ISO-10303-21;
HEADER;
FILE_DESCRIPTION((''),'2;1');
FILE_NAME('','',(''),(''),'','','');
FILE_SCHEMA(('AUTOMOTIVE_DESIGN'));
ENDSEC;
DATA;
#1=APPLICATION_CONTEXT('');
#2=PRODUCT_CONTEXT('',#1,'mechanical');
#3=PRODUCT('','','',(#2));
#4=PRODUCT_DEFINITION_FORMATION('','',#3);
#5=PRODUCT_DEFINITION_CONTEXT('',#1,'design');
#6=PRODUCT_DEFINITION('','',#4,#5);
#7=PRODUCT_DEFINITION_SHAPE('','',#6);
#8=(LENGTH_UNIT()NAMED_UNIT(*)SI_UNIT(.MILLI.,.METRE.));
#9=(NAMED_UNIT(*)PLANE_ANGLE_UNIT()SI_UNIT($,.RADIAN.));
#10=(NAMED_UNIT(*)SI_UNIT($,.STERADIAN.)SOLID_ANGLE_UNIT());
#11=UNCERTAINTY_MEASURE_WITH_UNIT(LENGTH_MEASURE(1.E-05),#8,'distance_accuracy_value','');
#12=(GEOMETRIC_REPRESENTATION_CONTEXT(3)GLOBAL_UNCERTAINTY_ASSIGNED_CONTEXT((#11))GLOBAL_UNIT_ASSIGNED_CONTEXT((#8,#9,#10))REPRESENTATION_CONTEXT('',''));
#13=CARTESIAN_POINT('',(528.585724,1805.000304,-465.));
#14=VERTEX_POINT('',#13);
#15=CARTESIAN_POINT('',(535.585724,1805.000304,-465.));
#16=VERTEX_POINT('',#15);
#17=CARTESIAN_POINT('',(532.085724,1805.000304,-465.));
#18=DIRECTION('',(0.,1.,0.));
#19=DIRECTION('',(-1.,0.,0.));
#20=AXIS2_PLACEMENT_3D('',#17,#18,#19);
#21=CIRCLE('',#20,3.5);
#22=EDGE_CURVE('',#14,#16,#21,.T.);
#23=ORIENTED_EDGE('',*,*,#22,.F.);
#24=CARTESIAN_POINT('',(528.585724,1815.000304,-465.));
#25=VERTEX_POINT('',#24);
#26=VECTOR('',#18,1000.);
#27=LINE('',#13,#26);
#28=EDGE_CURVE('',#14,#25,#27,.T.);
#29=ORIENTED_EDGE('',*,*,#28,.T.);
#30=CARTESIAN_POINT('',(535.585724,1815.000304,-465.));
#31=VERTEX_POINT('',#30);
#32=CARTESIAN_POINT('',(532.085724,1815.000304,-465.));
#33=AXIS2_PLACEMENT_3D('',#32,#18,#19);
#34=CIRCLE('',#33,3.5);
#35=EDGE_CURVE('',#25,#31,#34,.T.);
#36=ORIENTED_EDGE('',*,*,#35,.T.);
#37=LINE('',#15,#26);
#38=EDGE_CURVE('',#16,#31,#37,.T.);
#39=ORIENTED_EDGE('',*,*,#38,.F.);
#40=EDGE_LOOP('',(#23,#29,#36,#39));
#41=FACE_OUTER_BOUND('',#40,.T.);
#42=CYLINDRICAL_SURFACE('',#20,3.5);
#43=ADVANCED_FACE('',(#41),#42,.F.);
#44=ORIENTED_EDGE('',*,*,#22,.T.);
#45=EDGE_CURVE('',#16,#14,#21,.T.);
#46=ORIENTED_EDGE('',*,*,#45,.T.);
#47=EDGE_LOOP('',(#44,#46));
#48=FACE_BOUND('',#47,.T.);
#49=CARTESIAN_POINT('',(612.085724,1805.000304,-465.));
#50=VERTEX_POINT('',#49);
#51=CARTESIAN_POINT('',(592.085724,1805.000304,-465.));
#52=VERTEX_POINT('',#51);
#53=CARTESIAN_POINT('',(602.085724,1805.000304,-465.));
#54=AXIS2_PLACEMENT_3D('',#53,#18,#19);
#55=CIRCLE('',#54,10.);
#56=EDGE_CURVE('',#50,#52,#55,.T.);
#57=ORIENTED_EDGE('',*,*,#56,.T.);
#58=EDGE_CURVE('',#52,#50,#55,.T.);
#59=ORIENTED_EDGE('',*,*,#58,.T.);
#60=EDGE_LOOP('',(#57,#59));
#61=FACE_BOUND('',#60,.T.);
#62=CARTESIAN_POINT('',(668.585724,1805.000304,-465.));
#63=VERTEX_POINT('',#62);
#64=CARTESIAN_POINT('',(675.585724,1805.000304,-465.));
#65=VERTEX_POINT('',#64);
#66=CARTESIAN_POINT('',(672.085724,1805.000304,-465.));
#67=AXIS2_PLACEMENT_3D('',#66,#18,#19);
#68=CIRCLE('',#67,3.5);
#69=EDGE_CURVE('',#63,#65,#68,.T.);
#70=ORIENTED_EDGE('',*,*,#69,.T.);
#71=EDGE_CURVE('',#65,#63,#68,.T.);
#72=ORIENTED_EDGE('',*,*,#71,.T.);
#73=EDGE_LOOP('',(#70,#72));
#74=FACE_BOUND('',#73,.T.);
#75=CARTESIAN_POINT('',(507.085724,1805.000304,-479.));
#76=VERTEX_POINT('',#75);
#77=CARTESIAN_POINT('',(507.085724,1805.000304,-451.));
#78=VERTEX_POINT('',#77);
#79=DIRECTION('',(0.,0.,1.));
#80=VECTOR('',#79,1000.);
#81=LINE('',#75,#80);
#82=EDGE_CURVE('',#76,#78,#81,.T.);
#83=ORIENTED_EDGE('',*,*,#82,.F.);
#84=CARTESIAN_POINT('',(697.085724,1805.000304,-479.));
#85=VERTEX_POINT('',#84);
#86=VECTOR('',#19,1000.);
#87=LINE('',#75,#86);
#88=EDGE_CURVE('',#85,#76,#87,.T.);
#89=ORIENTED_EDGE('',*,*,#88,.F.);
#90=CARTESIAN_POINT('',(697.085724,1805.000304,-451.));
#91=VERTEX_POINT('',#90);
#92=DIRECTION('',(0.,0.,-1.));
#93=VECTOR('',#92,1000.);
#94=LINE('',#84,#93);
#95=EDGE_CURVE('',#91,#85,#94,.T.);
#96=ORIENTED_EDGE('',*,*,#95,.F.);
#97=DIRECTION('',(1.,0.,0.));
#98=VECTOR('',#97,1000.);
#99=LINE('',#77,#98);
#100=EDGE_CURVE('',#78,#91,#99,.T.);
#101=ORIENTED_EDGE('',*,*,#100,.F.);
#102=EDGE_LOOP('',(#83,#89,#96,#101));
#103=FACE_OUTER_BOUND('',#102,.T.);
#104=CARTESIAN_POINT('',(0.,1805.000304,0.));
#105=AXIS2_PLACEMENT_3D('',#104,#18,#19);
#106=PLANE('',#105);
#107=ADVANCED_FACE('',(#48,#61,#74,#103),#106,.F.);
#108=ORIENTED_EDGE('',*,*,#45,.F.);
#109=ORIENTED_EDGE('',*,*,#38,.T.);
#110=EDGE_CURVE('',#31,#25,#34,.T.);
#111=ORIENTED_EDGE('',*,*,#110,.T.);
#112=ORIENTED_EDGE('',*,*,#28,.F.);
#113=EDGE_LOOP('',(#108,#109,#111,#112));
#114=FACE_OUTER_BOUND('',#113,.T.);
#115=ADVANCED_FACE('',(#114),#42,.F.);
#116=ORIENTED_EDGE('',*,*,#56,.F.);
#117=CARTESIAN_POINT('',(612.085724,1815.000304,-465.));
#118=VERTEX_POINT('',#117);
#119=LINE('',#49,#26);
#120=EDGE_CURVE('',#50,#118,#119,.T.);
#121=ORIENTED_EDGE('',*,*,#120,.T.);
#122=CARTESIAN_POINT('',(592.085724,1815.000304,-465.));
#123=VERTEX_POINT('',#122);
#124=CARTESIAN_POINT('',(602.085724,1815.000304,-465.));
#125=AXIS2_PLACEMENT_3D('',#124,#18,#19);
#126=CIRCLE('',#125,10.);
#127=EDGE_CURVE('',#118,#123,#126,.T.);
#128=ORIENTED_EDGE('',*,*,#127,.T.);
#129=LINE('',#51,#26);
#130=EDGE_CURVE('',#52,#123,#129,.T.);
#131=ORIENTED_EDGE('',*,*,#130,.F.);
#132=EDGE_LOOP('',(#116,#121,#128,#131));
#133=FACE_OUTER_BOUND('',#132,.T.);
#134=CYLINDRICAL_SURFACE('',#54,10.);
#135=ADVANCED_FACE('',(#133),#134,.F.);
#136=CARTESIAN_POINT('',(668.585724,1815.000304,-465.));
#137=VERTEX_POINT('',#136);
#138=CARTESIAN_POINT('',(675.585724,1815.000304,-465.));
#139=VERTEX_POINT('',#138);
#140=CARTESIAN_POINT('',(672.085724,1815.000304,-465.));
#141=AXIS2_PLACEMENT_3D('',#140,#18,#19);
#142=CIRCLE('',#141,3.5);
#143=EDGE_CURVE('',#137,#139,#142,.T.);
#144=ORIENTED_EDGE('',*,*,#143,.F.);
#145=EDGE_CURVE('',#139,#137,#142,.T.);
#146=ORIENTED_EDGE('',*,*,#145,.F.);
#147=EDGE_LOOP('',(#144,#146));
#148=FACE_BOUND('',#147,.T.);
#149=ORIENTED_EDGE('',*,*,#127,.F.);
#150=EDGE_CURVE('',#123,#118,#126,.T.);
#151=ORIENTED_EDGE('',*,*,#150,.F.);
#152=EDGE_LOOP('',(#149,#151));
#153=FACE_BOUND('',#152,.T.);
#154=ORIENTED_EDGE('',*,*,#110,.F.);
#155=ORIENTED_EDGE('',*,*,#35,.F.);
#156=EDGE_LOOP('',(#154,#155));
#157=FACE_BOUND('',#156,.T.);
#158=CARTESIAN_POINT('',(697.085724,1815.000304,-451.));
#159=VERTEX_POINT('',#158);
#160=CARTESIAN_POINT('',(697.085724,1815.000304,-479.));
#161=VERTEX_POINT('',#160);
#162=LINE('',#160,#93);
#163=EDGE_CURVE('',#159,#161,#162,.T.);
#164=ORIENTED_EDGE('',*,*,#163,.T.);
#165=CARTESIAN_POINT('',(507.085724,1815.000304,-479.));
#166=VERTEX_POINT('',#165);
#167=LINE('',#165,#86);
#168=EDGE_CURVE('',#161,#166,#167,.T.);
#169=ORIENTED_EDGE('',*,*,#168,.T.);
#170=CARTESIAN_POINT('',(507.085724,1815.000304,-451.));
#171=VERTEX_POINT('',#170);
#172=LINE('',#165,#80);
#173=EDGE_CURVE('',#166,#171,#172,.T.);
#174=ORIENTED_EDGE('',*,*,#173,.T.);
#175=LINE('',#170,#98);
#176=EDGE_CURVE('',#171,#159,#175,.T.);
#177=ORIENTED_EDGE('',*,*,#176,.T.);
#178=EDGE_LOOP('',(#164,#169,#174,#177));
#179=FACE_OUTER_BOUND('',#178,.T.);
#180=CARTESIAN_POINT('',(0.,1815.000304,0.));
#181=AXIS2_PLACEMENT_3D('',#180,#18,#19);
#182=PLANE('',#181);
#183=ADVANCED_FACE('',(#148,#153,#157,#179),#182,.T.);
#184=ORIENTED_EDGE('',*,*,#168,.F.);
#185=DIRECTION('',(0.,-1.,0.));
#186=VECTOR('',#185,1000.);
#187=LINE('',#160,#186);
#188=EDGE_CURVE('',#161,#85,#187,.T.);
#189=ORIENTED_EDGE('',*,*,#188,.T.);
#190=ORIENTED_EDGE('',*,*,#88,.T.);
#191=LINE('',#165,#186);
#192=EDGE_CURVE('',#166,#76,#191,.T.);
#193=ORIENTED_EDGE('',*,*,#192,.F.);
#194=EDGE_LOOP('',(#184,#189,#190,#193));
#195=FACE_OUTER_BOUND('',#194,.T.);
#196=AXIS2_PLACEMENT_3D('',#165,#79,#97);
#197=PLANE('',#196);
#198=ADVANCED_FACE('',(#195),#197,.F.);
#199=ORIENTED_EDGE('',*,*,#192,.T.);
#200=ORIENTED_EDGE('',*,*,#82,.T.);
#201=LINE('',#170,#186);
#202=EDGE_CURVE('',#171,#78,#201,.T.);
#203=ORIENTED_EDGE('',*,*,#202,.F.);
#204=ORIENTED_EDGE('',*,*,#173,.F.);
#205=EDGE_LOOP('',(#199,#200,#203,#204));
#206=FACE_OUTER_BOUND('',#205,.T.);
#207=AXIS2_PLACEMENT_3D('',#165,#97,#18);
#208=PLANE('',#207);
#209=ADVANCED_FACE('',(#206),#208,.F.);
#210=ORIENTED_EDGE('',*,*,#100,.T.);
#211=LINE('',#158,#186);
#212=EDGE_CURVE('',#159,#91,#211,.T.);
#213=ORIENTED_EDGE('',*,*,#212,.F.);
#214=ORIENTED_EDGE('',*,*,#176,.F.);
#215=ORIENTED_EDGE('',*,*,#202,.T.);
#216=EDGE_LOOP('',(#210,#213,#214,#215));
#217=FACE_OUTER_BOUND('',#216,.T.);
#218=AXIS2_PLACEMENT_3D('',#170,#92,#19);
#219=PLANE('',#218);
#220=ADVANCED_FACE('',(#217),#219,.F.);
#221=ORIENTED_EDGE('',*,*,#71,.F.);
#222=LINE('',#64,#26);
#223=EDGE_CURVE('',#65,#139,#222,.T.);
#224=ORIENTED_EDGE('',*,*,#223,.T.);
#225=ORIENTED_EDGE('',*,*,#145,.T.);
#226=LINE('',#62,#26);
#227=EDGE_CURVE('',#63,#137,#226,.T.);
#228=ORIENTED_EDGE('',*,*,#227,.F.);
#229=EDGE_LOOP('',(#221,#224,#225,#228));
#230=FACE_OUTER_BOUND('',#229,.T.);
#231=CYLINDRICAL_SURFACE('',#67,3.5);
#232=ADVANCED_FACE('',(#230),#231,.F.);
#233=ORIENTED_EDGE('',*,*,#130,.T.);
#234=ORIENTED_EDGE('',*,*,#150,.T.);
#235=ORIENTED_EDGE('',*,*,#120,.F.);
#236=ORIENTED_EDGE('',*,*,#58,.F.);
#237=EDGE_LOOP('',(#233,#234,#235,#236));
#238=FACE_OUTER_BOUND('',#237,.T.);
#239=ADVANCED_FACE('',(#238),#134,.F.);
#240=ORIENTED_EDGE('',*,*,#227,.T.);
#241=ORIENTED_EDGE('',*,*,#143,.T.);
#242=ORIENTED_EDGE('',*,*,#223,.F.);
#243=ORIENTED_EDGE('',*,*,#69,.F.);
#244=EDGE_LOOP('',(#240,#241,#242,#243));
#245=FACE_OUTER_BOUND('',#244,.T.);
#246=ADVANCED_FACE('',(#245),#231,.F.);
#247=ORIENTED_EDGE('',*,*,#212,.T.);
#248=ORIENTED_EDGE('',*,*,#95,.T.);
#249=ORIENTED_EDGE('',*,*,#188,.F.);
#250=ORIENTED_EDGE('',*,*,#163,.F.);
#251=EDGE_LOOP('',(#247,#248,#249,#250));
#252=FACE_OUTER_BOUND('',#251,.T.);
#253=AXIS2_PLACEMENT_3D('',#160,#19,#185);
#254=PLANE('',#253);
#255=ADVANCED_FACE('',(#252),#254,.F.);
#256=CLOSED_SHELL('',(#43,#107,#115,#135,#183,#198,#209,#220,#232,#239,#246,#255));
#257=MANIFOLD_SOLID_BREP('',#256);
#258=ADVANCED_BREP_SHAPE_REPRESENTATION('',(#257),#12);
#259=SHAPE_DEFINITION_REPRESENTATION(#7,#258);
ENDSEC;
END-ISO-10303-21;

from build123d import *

# Parameters (mm, degrees)
SKETCH_1_W          = 190
SKETCH_1_H          = 28
EXTRUDE_1_DEPTH     = 10
SKETCH_2_R          = 3.5
SKETCH_2_R_2        = 10
CUT_EXTRUDE_1_DEPTH = 846.854305824


with BuildPart() as part:
    # 草图1 → 凸台-拉伸1 (new body)
    with BuildSketch(Plane(origin=(0, 1805.000303929, 0), x_dir=(1, 0, 0), z_dir=(0, 1, 0))):
        with Locations((602.085724054, 465)):
            Rectangle(SKETCH_1_W, SKETCH_1_H)
    extrude(amount=EXTRUDE_1_DEPTH)

    # 草图2 → 切除-拉伸1 (cut, through all)
    with BuildSketch(Plane(origin=(0, 1815.000303929, 0), x_dir=(1, 0, 0), z_dir=(0, 1, 0))):
        with Locations(Location((532.085724054, 465, 0), (0, 0, 180))):
            Circle(SKETCH_2_R)
        with Locations(Location((672.085724054, 465, 0), (0, 0, 180))):
            Circle(SKETCH_2_R)
        with Locations(Location((602.085724054, 465, 0), (0, 0, 180))):
            Circle(SKETCH_2_R_2)
    extrude(amount=-CUT_EXTRUDE_1_DEPTH, mode=Mode.SUBTRACT)


solid = part.part
